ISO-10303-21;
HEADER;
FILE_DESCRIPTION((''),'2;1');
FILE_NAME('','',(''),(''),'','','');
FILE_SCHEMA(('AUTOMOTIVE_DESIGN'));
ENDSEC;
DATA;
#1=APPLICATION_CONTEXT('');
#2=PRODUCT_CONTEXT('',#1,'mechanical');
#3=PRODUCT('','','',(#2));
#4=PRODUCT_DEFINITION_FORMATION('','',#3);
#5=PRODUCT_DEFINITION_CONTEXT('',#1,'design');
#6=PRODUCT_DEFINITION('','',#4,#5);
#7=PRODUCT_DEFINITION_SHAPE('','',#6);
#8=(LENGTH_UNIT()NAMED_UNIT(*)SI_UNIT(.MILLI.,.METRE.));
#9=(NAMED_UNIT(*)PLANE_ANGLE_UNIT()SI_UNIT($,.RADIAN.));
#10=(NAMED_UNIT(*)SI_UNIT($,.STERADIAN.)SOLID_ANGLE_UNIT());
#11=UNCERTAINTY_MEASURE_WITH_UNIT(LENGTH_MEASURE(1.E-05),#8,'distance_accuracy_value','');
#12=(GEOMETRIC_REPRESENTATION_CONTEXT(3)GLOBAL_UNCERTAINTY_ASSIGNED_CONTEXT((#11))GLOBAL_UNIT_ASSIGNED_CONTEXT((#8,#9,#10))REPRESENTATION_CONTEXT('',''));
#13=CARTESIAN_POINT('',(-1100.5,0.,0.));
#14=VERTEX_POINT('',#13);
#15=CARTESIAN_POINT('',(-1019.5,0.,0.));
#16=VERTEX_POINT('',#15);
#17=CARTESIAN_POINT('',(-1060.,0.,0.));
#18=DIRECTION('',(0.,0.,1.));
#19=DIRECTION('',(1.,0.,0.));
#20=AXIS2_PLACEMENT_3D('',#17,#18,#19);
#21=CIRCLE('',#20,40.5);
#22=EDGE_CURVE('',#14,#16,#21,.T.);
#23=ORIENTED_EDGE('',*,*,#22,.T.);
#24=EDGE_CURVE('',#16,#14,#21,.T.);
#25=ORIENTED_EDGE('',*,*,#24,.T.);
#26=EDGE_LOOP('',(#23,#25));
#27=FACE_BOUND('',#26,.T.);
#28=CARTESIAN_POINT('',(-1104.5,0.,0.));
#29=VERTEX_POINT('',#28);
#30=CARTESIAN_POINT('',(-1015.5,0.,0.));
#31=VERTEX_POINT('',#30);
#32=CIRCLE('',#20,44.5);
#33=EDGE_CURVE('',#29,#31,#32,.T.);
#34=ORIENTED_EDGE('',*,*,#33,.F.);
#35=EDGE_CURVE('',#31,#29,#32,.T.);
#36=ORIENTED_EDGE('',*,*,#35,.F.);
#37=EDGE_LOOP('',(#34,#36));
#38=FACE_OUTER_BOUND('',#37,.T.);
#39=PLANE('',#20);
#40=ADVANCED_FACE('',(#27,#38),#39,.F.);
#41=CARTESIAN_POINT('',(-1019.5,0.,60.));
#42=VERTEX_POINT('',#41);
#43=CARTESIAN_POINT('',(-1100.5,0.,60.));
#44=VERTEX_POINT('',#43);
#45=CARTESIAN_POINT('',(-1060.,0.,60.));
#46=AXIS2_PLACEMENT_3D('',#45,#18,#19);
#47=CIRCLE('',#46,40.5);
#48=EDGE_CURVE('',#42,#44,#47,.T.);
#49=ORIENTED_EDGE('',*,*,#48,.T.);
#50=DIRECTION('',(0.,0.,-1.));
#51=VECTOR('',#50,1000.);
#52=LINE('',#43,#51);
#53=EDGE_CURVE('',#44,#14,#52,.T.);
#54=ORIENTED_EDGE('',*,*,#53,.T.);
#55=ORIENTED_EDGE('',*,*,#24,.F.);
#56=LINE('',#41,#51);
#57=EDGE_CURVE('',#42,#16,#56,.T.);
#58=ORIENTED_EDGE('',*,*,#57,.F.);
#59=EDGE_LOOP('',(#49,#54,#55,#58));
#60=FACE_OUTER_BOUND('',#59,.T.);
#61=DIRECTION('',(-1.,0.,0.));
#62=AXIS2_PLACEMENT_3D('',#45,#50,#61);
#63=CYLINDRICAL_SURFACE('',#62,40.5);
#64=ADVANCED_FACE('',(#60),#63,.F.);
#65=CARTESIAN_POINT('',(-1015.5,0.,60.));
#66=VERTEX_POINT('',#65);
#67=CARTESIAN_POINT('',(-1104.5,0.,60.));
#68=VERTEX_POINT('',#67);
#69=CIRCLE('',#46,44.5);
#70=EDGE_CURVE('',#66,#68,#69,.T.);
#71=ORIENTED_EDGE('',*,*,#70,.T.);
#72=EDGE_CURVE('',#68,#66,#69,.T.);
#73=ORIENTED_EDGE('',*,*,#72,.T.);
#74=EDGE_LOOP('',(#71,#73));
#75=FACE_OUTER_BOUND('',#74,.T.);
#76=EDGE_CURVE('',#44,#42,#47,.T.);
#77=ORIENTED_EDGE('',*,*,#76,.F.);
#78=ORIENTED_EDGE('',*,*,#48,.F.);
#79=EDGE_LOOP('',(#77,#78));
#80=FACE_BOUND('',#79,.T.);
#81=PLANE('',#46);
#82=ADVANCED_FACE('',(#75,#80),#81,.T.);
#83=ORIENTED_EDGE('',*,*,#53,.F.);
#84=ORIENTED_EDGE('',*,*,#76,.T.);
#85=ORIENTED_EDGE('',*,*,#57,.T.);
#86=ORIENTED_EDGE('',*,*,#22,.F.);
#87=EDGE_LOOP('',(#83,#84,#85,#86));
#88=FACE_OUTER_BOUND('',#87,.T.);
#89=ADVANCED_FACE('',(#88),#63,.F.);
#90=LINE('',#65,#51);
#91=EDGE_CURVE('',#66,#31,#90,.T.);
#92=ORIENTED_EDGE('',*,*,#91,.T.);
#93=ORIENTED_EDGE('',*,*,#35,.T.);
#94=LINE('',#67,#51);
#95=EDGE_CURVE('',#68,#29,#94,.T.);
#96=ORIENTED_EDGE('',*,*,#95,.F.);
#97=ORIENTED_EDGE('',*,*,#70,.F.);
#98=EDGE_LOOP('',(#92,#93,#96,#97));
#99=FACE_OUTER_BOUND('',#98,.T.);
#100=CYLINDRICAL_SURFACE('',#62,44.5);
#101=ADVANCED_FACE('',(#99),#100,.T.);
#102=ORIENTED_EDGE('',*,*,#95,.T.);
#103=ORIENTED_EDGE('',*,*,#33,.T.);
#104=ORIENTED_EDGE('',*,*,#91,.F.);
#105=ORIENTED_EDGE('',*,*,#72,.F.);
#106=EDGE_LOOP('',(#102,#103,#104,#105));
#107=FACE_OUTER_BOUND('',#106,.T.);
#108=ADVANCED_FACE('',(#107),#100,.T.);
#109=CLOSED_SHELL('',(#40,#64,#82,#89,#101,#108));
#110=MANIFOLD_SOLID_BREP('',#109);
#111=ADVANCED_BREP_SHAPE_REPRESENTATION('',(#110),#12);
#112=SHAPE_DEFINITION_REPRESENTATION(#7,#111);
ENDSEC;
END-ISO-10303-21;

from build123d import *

# Parameters (mm, degrees)
SKETCH1_R           = 44.5
SKETCH1_R_2         = 40.5
BOSS_EXTRUDE1_DEPTH = 60


with BuildPart() as part:
    # Sketch1 → Boss-Extrude1 (new body)
    with BuildSketch(Plane.XY):
        with Locations((-1060, 0)):
            Circle(SKETCH1_R)
        with Locations((-1060, 0)):
            Circle(SKETCH1_R_2, mode=Mode.SUBTRACT)
    extrude(amount=BOSS_EXTRUDE1_DEPTH)


solid = part.part
